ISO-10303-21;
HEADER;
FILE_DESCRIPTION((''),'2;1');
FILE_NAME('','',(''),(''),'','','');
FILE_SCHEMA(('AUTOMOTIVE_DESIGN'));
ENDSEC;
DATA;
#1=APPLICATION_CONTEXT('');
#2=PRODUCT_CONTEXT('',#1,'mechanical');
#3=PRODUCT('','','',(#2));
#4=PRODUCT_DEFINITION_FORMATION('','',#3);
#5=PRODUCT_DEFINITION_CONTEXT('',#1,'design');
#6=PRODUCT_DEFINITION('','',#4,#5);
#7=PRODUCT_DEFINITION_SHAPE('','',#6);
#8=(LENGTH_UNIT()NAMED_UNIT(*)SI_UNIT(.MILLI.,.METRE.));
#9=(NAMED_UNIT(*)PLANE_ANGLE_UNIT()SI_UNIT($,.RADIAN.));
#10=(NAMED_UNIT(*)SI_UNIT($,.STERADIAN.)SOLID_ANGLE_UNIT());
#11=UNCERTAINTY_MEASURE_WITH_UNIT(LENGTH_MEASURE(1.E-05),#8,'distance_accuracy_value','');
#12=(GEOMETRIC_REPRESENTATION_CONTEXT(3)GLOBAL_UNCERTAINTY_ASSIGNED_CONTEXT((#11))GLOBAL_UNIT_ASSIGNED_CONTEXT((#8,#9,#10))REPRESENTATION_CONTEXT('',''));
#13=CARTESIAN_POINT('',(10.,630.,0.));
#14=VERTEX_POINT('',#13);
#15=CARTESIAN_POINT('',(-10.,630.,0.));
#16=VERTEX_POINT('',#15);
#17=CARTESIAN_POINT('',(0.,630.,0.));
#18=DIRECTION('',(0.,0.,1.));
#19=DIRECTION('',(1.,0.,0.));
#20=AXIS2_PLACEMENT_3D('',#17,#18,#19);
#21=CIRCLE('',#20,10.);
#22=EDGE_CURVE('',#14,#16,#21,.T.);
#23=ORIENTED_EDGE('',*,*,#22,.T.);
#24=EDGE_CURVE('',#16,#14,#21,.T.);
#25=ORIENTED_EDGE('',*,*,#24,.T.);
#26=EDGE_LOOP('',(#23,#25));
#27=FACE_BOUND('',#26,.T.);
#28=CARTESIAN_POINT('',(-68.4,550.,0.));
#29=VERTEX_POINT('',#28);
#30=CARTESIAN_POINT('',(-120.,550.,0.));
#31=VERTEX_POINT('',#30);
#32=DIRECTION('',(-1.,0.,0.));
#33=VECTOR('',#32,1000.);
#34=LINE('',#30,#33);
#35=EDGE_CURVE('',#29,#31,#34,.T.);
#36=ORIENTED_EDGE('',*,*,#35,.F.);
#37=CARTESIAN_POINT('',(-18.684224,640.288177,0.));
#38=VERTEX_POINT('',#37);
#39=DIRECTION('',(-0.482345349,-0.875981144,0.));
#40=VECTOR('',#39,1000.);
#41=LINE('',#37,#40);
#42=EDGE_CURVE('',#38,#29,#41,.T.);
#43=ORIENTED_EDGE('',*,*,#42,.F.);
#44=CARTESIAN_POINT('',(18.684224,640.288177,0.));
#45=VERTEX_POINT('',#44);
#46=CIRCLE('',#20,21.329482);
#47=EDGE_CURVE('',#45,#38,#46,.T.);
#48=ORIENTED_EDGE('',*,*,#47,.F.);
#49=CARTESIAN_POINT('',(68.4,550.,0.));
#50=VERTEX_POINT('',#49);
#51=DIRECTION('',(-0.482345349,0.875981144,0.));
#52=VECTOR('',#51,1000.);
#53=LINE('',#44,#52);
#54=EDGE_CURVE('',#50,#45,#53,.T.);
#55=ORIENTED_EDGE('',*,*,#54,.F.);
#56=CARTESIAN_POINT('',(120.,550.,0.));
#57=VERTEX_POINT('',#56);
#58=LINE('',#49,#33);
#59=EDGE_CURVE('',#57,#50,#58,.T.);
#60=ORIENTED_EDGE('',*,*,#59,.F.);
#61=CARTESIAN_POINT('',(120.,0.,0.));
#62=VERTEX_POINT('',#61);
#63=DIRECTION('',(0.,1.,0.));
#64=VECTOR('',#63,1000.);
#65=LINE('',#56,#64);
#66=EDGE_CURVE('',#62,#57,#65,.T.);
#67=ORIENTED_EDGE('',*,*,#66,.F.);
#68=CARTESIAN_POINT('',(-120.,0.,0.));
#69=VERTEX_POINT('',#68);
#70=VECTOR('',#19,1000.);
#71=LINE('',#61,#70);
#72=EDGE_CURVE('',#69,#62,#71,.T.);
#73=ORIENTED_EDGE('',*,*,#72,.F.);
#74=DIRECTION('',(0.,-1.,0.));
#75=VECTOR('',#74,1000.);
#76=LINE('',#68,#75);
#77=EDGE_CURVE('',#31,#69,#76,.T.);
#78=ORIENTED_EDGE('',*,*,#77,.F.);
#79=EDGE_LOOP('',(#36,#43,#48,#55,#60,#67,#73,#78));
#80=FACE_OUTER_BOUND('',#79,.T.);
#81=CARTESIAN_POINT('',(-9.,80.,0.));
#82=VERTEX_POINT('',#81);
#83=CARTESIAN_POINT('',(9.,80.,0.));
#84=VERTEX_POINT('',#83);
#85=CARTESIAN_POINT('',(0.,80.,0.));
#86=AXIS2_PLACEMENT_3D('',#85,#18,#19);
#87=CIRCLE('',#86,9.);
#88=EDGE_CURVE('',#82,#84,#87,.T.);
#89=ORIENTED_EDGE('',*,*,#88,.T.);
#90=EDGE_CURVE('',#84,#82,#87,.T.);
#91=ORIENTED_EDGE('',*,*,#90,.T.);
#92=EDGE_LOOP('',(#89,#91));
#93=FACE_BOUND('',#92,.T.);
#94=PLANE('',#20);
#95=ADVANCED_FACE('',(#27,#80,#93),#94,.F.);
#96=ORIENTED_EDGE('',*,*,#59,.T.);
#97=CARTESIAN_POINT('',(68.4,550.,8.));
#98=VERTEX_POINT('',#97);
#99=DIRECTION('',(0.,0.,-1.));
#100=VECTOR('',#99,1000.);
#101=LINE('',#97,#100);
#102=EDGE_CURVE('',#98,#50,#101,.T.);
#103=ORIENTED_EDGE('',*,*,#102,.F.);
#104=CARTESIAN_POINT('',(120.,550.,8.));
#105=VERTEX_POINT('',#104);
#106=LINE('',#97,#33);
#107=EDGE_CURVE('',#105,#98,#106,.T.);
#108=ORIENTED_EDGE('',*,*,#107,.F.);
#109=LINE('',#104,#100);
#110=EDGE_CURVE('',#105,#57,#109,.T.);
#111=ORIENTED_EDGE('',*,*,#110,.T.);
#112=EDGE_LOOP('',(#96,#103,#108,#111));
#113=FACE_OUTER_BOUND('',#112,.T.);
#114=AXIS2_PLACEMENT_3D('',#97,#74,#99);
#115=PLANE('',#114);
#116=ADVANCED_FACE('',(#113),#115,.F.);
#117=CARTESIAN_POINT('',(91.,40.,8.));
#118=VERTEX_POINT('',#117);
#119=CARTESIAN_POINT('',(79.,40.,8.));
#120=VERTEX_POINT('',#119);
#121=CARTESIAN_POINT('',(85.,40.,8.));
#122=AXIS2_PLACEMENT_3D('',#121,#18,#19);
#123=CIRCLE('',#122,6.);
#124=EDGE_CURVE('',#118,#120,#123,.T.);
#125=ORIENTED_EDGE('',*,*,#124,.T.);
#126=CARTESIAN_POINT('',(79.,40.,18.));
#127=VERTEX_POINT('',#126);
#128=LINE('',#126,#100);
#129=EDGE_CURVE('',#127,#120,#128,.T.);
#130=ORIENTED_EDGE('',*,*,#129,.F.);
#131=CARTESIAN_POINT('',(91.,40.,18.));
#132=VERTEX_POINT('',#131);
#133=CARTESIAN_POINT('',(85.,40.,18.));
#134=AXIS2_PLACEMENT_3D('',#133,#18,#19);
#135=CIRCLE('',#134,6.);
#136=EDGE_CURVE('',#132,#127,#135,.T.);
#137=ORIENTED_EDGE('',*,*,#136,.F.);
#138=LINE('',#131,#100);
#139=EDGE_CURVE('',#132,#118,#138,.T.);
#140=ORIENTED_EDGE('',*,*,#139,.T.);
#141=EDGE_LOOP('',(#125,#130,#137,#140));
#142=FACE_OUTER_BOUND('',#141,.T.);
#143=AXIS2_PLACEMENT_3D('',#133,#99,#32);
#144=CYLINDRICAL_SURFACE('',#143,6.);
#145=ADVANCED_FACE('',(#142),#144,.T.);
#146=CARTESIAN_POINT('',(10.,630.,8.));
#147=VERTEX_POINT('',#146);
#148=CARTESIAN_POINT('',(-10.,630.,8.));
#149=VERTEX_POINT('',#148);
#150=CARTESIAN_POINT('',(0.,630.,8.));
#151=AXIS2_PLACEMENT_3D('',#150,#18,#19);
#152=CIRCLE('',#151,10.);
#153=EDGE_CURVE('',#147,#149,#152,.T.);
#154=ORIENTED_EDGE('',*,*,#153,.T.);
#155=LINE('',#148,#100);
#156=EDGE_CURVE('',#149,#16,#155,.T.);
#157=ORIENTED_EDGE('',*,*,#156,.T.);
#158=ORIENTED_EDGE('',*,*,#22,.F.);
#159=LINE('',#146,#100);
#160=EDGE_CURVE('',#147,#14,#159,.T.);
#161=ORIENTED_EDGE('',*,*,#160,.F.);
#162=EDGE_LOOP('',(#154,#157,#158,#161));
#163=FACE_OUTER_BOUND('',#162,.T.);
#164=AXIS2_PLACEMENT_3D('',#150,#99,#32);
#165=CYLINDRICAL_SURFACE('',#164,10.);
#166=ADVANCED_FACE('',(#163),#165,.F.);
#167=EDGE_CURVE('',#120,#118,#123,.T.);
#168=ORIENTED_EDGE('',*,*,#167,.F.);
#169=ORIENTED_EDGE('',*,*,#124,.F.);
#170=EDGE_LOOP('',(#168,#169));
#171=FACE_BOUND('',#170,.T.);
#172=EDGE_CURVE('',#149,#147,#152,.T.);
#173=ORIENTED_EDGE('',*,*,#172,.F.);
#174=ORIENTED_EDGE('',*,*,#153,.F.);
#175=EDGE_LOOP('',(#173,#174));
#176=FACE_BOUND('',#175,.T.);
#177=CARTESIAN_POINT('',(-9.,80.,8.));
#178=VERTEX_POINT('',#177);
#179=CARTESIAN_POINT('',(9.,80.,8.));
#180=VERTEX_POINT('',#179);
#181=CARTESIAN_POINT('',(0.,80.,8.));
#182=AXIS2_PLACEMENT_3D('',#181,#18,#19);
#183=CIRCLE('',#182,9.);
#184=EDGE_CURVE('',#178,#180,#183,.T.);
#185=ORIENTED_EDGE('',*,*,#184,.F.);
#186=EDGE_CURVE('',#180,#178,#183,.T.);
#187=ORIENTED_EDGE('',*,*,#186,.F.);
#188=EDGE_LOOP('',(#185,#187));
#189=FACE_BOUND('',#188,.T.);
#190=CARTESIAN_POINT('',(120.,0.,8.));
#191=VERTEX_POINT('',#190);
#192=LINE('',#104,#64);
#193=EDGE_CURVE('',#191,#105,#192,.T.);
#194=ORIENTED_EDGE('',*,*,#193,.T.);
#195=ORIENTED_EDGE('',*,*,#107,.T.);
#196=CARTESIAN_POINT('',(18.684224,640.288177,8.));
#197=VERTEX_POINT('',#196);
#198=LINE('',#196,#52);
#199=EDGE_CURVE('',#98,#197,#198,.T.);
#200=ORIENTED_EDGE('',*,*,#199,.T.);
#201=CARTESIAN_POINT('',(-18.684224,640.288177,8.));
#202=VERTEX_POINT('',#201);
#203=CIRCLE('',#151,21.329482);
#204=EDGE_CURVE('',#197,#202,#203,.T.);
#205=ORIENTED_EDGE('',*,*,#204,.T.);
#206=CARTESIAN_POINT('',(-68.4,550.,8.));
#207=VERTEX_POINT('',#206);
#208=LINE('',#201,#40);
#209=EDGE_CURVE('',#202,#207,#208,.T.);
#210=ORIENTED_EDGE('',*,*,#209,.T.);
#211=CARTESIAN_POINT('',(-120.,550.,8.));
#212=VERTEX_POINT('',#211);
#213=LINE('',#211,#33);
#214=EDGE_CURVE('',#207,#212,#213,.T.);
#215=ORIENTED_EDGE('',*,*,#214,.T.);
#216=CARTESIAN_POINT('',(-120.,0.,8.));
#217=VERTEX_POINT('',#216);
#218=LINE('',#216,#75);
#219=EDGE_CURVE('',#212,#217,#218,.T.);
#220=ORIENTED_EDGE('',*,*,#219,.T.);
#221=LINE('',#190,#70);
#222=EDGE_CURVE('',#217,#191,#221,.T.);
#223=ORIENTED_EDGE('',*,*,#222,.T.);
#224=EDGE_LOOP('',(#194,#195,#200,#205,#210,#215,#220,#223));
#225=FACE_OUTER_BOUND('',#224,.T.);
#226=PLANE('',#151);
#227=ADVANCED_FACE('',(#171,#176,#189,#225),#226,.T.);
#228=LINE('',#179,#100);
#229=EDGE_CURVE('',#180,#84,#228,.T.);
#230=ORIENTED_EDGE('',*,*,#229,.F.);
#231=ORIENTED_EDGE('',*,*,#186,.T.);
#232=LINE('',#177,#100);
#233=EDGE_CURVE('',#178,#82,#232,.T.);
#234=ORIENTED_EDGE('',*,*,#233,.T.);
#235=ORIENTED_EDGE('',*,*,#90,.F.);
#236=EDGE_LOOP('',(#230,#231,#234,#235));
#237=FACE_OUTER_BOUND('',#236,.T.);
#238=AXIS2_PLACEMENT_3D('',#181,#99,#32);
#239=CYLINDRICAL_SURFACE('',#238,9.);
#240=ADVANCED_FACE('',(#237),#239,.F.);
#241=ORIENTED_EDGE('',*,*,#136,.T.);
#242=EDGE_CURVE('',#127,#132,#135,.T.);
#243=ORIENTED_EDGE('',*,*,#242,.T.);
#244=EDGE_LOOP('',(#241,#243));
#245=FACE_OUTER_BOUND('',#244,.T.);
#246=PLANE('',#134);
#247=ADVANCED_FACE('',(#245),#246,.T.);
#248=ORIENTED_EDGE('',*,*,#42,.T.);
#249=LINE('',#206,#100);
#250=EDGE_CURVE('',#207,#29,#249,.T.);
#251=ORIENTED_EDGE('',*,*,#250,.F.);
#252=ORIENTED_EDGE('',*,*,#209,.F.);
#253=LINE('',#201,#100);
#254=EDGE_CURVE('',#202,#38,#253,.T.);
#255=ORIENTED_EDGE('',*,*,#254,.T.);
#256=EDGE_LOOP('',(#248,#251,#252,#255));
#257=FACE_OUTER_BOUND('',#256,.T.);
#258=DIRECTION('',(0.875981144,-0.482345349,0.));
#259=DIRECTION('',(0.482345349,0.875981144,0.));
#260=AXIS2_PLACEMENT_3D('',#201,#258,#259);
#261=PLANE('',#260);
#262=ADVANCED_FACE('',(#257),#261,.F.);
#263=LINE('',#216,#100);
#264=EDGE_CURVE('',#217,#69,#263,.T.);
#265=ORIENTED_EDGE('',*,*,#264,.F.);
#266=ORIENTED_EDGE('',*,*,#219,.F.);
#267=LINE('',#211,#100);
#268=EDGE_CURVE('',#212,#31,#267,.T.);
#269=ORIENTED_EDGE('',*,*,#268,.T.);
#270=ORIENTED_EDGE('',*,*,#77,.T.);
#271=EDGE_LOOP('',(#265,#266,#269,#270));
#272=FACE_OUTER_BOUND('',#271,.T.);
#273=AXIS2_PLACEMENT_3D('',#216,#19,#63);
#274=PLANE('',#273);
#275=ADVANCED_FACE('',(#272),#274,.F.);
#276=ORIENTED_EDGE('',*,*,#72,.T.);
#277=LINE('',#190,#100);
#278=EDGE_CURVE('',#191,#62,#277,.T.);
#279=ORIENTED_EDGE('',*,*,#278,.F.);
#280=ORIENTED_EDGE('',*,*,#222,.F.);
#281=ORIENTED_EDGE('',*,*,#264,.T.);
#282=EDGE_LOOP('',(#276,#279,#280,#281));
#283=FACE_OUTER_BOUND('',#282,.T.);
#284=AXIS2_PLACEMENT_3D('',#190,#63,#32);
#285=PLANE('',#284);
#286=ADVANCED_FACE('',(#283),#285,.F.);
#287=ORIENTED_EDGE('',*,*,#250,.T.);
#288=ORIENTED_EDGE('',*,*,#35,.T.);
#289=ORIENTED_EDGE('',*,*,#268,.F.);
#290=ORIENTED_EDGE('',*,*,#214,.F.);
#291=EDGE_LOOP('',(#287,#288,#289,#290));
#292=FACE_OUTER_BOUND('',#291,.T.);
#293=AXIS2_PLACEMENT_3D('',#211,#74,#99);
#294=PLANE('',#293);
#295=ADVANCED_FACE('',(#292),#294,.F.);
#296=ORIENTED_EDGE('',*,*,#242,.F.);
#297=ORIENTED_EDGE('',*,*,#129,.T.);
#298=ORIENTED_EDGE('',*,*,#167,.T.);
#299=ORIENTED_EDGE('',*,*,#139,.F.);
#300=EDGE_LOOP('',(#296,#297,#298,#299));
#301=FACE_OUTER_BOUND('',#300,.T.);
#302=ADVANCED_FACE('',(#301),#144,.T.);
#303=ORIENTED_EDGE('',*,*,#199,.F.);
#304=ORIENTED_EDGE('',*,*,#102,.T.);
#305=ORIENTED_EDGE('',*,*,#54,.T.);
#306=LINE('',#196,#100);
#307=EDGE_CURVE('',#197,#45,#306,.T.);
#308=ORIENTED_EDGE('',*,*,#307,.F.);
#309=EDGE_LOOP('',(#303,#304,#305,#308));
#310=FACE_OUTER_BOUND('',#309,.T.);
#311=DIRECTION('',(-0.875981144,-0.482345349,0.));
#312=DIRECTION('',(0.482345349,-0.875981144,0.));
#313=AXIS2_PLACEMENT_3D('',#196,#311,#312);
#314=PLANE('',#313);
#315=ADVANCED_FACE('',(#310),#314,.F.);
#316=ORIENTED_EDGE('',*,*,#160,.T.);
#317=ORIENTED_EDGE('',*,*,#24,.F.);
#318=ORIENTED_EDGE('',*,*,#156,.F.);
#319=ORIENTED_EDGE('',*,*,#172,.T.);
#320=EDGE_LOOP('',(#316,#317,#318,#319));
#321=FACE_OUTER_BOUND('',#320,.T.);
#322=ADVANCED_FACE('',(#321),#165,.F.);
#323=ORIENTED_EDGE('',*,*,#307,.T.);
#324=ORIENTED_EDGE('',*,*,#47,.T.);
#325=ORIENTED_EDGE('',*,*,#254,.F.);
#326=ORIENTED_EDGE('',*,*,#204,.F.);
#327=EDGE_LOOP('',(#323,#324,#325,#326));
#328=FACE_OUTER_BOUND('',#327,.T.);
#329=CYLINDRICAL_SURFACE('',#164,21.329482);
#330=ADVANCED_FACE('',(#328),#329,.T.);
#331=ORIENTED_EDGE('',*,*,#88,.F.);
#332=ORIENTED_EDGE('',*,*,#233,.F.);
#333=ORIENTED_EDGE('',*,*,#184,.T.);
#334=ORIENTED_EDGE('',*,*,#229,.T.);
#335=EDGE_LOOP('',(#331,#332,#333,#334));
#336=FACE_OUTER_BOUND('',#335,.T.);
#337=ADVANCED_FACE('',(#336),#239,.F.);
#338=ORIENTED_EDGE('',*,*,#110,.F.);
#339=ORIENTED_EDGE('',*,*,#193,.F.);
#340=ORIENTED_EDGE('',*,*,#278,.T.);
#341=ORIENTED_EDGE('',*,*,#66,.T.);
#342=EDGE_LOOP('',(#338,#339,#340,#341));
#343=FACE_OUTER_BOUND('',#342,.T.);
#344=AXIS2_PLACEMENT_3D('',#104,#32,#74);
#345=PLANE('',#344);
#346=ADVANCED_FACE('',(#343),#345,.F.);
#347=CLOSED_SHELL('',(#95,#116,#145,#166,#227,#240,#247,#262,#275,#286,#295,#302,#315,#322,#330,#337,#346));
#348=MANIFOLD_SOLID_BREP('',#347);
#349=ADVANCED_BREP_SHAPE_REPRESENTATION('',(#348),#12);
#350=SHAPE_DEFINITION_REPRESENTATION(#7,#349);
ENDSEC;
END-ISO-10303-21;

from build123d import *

# Parameters (mm, degrees)
SKETCH1_R           = 10
SKETCH1_R_2         = 9
BOSS_EXTRUDE1_DEPTH = 8
SKETCH2_R           = 6
BOSS_EXTRUDE2_DEPTH = 10


with BuildPart() as part:
    # Sketch1 → Boss-Extrude1 (new body)
    with BuildSketch(Plane.XY):
        with BuildLine():
            Line((-120, 550), (-68.4, 550))
            Line((-68.4, 550), (-18.684224353, 640.288176603))
            ThreePointArc((-18.684224353, 640.288176603), (0, 651.329482354), (18.684224353, 640.288176603))
            Line((18.684224353, 640.288176603), (68.4, 550))
            Line((68.4, 550), (120, 550))
            Line((120, 550), (120, 0))
            Line((120, 0), (-120, 0))
            Line((-120, 0), (-120, 550))
        make_face()
        with Locations((0, 630)):
            Circle(SKETCH1_R, mode=Mode.SUBTRACT)
        with Locations((0, 80)):
            Circle(SKETCH1_R_2, mode=Mode.SUBTRACT)
    extrude(amount=BOSS_EXTRUDE1_DEPTH)

    # Sketch2 → Boss-Extrude2 (add)
    with BuildSketch(Plane.XY.offset(8)):
        with Locations((85, 40)):
            Circle(SKETCH2_R)
    extrude(amount=BOSS_EXTRUDE2_DEPTH)


solid = part.part
